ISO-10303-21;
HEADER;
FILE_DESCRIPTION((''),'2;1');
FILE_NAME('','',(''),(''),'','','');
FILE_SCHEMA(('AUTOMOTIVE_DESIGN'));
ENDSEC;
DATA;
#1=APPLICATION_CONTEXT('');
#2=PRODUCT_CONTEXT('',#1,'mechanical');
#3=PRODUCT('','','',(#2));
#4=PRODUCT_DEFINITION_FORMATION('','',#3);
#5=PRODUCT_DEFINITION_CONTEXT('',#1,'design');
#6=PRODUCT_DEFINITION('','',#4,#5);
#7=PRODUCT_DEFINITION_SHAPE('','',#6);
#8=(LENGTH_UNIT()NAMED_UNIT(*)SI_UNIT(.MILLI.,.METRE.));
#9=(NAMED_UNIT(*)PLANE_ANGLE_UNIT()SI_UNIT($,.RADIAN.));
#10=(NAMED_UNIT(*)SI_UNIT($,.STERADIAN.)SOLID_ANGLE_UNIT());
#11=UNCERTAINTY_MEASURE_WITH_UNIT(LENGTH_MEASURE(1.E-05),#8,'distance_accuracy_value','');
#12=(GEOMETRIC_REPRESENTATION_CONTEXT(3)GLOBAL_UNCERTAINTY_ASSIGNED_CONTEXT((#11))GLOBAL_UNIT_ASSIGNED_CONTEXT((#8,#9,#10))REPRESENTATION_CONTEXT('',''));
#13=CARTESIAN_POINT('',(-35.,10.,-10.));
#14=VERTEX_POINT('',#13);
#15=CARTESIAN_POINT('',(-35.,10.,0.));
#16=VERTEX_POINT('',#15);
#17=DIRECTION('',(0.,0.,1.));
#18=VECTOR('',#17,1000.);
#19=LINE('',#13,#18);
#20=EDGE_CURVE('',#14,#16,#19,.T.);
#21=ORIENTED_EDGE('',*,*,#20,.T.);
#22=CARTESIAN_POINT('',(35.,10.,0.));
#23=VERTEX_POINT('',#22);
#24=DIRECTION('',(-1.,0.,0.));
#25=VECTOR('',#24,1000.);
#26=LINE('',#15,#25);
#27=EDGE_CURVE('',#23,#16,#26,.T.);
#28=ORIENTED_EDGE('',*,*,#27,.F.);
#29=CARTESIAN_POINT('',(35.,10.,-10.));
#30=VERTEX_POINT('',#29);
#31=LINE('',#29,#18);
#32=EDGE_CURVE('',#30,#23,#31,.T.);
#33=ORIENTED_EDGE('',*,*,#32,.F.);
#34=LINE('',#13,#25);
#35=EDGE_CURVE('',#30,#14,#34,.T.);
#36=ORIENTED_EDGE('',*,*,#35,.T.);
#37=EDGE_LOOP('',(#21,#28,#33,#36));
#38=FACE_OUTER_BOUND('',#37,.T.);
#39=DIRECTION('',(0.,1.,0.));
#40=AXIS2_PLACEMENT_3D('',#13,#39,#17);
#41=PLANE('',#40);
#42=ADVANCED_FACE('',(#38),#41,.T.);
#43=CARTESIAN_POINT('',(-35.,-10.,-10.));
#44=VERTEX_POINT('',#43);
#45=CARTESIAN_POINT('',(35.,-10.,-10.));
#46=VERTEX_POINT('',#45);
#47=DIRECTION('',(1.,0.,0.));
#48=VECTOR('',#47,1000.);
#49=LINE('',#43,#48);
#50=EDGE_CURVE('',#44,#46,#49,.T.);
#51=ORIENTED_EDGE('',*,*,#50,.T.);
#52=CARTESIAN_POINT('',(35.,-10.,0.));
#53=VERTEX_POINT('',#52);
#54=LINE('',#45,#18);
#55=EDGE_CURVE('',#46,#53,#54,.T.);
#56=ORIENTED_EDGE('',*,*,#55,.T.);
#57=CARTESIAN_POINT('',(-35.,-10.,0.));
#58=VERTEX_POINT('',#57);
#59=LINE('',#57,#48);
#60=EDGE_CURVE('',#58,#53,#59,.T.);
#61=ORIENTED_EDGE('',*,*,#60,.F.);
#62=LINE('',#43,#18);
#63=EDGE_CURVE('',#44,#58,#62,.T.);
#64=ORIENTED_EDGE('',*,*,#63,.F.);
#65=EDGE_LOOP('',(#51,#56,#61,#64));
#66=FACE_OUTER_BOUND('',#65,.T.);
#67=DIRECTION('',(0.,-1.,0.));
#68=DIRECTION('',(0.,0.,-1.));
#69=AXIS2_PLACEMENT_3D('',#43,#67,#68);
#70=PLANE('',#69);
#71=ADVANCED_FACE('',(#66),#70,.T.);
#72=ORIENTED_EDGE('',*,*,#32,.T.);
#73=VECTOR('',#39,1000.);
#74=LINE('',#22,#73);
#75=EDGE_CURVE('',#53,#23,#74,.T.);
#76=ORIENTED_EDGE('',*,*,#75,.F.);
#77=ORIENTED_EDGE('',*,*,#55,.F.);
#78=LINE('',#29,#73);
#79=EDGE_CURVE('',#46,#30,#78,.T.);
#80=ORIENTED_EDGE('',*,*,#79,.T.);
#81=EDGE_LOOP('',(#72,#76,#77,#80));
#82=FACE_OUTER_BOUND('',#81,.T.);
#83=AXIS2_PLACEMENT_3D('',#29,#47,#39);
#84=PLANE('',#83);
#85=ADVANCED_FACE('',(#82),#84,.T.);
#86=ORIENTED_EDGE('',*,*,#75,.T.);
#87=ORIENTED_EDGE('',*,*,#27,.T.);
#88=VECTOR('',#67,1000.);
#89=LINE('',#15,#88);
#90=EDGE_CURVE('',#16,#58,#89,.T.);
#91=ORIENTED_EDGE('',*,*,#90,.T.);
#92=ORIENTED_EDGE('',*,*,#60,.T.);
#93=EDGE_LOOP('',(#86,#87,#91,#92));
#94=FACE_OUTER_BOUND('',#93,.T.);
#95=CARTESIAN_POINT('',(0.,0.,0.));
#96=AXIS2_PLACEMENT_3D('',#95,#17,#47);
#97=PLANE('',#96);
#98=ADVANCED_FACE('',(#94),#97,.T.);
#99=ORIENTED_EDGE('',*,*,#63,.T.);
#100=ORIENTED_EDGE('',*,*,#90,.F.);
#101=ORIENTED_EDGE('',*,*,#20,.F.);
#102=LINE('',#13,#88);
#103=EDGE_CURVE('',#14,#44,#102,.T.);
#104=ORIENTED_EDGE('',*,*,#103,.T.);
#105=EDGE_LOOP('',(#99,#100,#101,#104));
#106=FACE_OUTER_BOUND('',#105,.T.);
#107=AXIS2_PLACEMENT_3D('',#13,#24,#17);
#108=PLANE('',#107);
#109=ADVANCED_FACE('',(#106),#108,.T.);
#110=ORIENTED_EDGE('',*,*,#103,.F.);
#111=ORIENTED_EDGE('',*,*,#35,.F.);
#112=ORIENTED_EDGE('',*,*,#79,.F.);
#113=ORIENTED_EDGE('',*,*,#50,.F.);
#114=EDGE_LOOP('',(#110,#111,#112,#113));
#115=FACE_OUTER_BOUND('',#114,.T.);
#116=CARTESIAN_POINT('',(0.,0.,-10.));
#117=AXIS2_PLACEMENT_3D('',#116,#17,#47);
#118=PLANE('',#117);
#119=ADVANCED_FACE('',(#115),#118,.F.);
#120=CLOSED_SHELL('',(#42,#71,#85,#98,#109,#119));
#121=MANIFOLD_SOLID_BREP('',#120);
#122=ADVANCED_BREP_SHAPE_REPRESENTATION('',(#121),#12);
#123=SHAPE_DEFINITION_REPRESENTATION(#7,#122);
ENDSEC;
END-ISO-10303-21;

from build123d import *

# Parameters (mm, degrees)
SKETCH_1_W      = 70
SKETCH_1_H      = 20
EXTRUDE_1_DEPTH = 10


with BuildPart() as part:
    # 草图1 → 凸台-拉伸1 (new body)
    with BuildSketch(Plane.XY):
        Rectangle(SKETCH_1_W, SKETCH_1_H)
    extrude(amount=-EXTRUDE_1_DEPTH)


solid = part.part
